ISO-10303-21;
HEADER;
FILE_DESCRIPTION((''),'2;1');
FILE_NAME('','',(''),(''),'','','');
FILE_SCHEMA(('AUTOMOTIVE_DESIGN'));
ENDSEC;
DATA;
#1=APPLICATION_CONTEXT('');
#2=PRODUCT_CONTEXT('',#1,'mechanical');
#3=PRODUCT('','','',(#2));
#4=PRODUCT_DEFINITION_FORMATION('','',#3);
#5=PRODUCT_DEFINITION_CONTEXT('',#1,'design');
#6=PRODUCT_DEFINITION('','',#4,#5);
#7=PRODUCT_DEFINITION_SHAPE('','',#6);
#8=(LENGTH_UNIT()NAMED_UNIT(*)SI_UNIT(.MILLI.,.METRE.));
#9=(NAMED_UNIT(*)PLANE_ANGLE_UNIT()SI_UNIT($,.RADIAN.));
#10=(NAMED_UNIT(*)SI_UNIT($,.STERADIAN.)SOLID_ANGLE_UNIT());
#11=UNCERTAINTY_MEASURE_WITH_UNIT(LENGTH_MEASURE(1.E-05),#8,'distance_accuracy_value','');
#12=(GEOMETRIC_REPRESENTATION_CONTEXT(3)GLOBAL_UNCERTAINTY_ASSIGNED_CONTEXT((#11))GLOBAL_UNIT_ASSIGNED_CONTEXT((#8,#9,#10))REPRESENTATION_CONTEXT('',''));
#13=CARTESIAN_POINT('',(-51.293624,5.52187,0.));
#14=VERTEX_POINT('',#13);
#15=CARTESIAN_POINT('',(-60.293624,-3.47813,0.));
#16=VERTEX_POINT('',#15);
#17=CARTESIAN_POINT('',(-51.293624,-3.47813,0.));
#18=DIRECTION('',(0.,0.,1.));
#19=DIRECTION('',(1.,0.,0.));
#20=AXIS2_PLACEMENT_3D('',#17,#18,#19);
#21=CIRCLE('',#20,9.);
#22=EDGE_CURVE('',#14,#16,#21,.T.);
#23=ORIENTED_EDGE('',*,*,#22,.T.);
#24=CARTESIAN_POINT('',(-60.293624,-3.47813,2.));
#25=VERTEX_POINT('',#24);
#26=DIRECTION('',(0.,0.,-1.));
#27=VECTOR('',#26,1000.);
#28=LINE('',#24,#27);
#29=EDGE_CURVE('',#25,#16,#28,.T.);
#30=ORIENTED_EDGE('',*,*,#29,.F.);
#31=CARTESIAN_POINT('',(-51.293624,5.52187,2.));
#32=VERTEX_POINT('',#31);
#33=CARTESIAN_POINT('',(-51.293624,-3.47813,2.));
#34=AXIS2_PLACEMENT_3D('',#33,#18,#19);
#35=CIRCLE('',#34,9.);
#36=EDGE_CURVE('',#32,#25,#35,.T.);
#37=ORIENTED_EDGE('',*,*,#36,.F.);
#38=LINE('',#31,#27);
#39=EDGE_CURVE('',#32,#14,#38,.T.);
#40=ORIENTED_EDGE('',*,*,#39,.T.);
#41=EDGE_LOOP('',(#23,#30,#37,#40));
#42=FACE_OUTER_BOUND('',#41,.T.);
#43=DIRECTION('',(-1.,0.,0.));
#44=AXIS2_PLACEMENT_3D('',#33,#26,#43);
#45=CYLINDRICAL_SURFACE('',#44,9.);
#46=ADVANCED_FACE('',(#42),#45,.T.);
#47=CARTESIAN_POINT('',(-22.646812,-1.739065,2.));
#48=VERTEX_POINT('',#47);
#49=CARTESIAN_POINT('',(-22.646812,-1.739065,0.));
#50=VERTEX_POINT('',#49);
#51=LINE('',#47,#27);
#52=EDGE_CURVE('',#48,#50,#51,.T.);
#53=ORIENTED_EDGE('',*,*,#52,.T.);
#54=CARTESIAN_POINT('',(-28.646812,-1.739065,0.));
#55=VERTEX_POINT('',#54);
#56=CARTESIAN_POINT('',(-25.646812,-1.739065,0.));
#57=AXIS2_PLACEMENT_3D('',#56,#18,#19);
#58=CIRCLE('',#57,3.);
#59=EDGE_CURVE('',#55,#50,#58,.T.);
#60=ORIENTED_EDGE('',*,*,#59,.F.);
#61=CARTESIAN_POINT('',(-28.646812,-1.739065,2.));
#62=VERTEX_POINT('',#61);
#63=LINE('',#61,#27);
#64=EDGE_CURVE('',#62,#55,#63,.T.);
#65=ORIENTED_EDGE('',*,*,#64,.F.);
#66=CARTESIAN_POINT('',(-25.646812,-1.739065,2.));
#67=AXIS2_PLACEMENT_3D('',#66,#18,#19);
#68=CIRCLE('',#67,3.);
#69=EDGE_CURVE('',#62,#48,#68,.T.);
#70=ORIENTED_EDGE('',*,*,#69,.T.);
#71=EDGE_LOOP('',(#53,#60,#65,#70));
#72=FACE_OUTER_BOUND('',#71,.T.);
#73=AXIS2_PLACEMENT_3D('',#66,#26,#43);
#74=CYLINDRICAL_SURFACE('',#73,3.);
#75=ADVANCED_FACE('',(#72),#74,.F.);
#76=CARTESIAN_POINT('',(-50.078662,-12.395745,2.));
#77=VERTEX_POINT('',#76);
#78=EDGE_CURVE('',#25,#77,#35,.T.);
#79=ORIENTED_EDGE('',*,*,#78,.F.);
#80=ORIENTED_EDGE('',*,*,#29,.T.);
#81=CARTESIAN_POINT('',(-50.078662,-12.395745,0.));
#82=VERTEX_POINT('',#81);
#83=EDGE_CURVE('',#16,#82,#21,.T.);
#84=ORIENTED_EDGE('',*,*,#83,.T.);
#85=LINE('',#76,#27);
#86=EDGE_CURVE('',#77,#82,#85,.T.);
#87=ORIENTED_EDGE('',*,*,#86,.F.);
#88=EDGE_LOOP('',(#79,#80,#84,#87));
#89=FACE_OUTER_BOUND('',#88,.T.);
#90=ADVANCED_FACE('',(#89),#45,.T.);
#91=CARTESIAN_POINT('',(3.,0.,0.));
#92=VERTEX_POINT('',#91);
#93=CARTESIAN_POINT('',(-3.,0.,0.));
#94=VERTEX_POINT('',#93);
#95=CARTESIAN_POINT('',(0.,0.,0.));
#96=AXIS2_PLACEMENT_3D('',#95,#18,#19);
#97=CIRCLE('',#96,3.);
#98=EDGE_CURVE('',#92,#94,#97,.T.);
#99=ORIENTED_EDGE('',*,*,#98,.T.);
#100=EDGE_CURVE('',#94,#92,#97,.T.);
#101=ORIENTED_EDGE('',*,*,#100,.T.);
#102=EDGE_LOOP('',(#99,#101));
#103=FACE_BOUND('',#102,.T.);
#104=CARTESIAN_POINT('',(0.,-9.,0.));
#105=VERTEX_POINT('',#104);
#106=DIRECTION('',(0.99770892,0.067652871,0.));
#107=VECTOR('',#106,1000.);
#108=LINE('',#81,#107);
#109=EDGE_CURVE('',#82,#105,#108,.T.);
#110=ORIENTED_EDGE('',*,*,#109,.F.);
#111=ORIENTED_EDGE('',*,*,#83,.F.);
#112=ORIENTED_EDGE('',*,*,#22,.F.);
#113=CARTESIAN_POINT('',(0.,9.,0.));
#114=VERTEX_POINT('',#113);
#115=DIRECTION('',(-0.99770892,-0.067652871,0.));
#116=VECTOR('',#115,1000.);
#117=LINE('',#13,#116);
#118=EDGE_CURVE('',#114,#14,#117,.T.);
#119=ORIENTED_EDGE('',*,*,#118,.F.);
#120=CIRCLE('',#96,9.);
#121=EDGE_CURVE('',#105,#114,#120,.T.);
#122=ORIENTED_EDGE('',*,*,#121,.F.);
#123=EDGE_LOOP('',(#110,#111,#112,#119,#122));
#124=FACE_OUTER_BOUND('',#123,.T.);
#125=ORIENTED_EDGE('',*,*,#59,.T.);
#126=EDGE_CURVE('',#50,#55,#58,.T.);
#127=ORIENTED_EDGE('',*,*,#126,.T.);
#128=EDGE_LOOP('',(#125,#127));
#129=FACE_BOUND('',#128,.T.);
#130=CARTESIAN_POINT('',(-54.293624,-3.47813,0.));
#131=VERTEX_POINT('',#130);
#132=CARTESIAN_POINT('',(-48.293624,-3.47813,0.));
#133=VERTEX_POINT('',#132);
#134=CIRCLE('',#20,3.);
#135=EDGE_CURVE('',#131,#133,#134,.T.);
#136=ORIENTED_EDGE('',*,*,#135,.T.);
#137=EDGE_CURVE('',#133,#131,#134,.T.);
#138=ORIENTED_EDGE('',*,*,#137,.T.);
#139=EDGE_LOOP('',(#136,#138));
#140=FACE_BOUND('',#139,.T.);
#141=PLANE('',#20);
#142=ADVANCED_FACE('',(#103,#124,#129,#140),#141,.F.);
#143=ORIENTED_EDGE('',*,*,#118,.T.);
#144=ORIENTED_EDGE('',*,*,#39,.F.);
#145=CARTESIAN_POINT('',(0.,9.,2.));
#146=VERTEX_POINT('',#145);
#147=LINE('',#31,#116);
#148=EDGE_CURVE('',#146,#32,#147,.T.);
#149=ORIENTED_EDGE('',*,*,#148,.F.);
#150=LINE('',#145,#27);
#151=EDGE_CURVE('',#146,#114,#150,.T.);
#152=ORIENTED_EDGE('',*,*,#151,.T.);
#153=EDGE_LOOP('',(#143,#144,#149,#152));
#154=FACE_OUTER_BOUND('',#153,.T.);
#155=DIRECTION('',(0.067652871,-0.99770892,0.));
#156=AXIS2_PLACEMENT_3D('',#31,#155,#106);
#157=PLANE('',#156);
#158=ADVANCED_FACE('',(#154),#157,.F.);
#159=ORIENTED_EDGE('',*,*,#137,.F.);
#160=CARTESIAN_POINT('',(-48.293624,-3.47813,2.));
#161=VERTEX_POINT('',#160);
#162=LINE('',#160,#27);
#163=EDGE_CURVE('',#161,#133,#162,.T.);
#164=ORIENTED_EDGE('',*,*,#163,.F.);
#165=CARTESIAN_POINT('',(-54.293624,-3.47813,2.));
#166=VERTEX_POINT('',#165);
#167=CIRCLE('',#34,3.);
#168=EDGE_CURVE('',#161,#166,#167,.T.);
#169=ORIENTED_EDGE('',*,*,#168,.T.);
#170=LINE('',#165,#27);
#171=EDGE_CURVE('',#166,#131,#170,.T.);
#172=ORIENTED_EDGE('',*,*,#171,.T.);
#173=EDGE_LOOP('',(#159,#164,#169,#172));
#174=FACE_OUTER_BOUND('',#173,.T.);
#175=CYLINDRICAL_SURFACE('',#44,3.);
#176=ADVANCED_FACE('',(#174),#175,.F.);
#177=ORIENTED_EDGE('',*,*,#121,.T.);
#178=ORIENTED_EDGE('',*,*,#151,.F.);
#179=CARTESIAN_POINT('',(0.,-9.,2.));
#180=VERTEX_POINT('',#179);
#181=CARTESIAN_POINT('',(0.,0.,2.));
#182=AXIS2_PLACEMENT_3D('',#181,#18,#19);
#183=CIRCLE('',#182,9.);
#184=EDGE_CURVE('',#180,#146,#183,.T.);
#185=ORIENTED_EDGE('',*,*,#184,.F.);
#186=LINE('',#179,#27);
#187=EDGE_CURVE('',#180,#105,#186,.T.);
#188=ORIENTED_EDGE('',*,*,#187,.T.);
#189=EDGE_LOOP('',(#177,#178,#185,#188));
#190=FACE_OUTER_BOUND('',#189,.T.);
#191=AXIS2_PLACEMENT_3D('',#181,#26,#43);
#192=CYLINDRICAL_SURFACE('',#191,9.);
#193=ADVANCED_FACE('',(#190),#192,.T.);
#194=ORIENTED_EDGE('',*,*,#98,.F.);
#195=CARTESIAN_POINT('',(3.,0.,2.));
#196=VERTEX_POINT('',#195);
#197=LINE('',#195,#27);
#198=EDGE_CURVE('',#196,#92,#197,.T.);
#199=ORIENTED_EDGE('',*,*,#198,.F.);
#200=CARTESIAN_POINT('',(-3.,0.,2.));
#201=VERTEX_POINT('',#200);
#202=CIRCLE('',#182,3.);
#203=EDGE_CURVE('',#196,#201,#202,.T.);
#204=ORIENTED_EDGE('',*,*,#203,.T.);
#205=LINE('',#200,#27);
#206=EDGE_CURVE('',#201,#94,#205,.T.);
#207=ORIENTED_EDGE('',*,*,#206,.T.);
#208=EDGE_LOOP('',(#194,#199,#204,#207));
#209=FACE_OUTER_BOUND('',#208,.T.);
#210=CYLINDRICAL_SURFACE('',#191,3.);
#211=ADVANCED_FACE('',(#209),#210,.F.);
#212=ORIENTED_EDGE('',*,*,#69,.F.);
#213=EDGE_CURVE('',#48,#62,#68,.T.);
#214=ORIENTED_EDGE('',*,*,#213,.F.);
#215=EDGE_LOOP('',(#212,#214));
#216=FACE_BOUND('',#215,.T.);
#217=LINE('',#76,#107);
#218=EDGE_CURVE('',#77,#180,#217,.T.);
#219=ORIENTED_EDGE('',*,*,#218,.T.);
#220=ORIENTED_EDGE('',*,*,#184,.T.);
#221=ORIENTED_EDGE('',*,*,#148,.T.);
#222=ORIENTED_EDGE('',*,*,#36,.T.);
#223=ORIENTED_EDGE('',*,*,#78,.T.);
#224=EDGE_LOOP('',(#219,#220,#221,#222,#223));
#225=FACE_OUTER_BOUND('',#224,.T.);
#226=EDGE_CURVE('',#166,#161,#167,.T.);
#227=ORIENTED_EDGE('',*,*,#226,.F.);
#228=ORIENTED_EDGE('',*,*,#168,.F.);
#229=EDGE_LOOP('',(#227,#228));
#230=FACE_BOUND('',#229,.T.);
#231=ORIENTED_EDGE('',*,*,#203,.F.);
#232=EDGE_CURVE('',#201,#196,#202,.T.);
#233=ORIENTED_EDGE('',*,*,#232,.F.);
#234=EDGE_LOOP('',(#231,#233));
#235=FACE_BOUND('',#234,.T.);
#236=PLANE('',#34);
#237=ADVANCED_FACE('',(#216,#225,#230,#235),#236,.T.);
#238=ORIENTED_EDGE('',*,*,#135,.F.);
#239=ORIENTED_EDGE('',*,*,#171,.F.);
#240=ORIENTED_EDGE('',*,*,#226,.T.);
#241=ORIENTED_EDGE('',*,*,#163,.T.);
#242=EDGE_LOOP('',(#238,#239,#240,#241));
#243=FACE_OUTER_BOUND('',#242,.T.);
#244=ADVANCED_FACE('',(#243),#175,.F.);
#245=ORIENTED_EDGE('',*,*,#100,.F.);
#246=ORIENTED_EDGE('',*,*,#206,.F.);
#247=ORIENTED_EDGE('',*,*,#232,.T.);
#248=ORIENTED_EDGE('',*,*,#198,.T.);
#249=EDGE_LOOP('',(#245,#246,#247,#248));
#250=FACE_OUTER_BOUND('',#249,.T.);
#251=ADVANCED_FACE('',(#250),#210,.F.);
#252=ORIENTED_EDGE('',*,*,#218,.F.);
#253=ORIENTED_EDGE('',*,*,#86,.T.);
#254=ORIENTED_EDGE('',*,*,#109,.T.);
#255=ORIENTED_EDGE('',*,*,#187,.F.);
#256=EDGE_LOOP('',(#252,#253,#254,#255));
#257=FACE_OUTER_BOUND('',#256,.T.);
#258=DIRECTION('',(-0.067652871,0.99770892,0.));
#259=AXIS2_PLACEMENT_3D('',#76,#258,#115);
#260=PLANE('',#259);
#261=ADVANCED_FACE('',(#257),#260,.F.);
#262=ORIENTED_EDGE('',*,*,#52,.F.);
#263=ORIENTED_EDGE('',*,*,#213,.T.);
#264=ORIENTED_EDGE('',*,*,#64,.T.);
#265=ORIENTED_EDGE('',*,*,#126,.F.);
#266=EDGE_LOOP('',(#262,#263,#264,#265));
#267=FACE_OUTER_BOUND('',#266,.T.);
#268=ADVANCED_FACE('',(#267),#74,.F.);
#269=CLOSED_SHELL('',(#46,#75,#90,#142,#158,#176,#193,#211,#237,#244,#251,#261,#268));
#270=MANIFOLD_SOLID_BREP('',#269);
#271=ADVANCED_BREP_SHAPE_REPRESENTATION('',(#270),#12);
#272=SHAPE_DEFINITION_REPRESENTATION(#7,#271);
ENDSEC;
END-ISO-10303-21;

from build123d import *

# Parameters (mm, degrees)
SKETCH1_R           = 3
BOSS_EXTRUDE1_DEPTH = 2


with BuildPart() as part:
    # Sketch1 → Boss-Extrude1 (new body)
    with BuildSketch(Plane.XY):
        with BuildLine():
            Line((-51.293623615, 5.521870404), (0, 9))
            ThreePointArc((0, 9), (9, 0), (0, -9))
            Line((0, -9), (-50.078661895, -12.395745198))
            ThreePointArc((-50.078661895, -12.395745198), (-60.273003894, -4.087005439), (-51.293623615, 5.521870404))
        make_face()
        with Locations((-51.293623615, -3.478129596)):
            Circle(SKETCH1_R, mode=Mode.SUBTRACT)
        Circle(SKETCH1_R, mode=Mode.SUBTRACT)
        with Locations((-25.646811807, -1.739064798)):
            Circle(SKETCH1_R, mode=Mode.SUBTRACT)
    extrude(amount=BOSS_EXTRUDE1_DEPTH)


solid = part.part
